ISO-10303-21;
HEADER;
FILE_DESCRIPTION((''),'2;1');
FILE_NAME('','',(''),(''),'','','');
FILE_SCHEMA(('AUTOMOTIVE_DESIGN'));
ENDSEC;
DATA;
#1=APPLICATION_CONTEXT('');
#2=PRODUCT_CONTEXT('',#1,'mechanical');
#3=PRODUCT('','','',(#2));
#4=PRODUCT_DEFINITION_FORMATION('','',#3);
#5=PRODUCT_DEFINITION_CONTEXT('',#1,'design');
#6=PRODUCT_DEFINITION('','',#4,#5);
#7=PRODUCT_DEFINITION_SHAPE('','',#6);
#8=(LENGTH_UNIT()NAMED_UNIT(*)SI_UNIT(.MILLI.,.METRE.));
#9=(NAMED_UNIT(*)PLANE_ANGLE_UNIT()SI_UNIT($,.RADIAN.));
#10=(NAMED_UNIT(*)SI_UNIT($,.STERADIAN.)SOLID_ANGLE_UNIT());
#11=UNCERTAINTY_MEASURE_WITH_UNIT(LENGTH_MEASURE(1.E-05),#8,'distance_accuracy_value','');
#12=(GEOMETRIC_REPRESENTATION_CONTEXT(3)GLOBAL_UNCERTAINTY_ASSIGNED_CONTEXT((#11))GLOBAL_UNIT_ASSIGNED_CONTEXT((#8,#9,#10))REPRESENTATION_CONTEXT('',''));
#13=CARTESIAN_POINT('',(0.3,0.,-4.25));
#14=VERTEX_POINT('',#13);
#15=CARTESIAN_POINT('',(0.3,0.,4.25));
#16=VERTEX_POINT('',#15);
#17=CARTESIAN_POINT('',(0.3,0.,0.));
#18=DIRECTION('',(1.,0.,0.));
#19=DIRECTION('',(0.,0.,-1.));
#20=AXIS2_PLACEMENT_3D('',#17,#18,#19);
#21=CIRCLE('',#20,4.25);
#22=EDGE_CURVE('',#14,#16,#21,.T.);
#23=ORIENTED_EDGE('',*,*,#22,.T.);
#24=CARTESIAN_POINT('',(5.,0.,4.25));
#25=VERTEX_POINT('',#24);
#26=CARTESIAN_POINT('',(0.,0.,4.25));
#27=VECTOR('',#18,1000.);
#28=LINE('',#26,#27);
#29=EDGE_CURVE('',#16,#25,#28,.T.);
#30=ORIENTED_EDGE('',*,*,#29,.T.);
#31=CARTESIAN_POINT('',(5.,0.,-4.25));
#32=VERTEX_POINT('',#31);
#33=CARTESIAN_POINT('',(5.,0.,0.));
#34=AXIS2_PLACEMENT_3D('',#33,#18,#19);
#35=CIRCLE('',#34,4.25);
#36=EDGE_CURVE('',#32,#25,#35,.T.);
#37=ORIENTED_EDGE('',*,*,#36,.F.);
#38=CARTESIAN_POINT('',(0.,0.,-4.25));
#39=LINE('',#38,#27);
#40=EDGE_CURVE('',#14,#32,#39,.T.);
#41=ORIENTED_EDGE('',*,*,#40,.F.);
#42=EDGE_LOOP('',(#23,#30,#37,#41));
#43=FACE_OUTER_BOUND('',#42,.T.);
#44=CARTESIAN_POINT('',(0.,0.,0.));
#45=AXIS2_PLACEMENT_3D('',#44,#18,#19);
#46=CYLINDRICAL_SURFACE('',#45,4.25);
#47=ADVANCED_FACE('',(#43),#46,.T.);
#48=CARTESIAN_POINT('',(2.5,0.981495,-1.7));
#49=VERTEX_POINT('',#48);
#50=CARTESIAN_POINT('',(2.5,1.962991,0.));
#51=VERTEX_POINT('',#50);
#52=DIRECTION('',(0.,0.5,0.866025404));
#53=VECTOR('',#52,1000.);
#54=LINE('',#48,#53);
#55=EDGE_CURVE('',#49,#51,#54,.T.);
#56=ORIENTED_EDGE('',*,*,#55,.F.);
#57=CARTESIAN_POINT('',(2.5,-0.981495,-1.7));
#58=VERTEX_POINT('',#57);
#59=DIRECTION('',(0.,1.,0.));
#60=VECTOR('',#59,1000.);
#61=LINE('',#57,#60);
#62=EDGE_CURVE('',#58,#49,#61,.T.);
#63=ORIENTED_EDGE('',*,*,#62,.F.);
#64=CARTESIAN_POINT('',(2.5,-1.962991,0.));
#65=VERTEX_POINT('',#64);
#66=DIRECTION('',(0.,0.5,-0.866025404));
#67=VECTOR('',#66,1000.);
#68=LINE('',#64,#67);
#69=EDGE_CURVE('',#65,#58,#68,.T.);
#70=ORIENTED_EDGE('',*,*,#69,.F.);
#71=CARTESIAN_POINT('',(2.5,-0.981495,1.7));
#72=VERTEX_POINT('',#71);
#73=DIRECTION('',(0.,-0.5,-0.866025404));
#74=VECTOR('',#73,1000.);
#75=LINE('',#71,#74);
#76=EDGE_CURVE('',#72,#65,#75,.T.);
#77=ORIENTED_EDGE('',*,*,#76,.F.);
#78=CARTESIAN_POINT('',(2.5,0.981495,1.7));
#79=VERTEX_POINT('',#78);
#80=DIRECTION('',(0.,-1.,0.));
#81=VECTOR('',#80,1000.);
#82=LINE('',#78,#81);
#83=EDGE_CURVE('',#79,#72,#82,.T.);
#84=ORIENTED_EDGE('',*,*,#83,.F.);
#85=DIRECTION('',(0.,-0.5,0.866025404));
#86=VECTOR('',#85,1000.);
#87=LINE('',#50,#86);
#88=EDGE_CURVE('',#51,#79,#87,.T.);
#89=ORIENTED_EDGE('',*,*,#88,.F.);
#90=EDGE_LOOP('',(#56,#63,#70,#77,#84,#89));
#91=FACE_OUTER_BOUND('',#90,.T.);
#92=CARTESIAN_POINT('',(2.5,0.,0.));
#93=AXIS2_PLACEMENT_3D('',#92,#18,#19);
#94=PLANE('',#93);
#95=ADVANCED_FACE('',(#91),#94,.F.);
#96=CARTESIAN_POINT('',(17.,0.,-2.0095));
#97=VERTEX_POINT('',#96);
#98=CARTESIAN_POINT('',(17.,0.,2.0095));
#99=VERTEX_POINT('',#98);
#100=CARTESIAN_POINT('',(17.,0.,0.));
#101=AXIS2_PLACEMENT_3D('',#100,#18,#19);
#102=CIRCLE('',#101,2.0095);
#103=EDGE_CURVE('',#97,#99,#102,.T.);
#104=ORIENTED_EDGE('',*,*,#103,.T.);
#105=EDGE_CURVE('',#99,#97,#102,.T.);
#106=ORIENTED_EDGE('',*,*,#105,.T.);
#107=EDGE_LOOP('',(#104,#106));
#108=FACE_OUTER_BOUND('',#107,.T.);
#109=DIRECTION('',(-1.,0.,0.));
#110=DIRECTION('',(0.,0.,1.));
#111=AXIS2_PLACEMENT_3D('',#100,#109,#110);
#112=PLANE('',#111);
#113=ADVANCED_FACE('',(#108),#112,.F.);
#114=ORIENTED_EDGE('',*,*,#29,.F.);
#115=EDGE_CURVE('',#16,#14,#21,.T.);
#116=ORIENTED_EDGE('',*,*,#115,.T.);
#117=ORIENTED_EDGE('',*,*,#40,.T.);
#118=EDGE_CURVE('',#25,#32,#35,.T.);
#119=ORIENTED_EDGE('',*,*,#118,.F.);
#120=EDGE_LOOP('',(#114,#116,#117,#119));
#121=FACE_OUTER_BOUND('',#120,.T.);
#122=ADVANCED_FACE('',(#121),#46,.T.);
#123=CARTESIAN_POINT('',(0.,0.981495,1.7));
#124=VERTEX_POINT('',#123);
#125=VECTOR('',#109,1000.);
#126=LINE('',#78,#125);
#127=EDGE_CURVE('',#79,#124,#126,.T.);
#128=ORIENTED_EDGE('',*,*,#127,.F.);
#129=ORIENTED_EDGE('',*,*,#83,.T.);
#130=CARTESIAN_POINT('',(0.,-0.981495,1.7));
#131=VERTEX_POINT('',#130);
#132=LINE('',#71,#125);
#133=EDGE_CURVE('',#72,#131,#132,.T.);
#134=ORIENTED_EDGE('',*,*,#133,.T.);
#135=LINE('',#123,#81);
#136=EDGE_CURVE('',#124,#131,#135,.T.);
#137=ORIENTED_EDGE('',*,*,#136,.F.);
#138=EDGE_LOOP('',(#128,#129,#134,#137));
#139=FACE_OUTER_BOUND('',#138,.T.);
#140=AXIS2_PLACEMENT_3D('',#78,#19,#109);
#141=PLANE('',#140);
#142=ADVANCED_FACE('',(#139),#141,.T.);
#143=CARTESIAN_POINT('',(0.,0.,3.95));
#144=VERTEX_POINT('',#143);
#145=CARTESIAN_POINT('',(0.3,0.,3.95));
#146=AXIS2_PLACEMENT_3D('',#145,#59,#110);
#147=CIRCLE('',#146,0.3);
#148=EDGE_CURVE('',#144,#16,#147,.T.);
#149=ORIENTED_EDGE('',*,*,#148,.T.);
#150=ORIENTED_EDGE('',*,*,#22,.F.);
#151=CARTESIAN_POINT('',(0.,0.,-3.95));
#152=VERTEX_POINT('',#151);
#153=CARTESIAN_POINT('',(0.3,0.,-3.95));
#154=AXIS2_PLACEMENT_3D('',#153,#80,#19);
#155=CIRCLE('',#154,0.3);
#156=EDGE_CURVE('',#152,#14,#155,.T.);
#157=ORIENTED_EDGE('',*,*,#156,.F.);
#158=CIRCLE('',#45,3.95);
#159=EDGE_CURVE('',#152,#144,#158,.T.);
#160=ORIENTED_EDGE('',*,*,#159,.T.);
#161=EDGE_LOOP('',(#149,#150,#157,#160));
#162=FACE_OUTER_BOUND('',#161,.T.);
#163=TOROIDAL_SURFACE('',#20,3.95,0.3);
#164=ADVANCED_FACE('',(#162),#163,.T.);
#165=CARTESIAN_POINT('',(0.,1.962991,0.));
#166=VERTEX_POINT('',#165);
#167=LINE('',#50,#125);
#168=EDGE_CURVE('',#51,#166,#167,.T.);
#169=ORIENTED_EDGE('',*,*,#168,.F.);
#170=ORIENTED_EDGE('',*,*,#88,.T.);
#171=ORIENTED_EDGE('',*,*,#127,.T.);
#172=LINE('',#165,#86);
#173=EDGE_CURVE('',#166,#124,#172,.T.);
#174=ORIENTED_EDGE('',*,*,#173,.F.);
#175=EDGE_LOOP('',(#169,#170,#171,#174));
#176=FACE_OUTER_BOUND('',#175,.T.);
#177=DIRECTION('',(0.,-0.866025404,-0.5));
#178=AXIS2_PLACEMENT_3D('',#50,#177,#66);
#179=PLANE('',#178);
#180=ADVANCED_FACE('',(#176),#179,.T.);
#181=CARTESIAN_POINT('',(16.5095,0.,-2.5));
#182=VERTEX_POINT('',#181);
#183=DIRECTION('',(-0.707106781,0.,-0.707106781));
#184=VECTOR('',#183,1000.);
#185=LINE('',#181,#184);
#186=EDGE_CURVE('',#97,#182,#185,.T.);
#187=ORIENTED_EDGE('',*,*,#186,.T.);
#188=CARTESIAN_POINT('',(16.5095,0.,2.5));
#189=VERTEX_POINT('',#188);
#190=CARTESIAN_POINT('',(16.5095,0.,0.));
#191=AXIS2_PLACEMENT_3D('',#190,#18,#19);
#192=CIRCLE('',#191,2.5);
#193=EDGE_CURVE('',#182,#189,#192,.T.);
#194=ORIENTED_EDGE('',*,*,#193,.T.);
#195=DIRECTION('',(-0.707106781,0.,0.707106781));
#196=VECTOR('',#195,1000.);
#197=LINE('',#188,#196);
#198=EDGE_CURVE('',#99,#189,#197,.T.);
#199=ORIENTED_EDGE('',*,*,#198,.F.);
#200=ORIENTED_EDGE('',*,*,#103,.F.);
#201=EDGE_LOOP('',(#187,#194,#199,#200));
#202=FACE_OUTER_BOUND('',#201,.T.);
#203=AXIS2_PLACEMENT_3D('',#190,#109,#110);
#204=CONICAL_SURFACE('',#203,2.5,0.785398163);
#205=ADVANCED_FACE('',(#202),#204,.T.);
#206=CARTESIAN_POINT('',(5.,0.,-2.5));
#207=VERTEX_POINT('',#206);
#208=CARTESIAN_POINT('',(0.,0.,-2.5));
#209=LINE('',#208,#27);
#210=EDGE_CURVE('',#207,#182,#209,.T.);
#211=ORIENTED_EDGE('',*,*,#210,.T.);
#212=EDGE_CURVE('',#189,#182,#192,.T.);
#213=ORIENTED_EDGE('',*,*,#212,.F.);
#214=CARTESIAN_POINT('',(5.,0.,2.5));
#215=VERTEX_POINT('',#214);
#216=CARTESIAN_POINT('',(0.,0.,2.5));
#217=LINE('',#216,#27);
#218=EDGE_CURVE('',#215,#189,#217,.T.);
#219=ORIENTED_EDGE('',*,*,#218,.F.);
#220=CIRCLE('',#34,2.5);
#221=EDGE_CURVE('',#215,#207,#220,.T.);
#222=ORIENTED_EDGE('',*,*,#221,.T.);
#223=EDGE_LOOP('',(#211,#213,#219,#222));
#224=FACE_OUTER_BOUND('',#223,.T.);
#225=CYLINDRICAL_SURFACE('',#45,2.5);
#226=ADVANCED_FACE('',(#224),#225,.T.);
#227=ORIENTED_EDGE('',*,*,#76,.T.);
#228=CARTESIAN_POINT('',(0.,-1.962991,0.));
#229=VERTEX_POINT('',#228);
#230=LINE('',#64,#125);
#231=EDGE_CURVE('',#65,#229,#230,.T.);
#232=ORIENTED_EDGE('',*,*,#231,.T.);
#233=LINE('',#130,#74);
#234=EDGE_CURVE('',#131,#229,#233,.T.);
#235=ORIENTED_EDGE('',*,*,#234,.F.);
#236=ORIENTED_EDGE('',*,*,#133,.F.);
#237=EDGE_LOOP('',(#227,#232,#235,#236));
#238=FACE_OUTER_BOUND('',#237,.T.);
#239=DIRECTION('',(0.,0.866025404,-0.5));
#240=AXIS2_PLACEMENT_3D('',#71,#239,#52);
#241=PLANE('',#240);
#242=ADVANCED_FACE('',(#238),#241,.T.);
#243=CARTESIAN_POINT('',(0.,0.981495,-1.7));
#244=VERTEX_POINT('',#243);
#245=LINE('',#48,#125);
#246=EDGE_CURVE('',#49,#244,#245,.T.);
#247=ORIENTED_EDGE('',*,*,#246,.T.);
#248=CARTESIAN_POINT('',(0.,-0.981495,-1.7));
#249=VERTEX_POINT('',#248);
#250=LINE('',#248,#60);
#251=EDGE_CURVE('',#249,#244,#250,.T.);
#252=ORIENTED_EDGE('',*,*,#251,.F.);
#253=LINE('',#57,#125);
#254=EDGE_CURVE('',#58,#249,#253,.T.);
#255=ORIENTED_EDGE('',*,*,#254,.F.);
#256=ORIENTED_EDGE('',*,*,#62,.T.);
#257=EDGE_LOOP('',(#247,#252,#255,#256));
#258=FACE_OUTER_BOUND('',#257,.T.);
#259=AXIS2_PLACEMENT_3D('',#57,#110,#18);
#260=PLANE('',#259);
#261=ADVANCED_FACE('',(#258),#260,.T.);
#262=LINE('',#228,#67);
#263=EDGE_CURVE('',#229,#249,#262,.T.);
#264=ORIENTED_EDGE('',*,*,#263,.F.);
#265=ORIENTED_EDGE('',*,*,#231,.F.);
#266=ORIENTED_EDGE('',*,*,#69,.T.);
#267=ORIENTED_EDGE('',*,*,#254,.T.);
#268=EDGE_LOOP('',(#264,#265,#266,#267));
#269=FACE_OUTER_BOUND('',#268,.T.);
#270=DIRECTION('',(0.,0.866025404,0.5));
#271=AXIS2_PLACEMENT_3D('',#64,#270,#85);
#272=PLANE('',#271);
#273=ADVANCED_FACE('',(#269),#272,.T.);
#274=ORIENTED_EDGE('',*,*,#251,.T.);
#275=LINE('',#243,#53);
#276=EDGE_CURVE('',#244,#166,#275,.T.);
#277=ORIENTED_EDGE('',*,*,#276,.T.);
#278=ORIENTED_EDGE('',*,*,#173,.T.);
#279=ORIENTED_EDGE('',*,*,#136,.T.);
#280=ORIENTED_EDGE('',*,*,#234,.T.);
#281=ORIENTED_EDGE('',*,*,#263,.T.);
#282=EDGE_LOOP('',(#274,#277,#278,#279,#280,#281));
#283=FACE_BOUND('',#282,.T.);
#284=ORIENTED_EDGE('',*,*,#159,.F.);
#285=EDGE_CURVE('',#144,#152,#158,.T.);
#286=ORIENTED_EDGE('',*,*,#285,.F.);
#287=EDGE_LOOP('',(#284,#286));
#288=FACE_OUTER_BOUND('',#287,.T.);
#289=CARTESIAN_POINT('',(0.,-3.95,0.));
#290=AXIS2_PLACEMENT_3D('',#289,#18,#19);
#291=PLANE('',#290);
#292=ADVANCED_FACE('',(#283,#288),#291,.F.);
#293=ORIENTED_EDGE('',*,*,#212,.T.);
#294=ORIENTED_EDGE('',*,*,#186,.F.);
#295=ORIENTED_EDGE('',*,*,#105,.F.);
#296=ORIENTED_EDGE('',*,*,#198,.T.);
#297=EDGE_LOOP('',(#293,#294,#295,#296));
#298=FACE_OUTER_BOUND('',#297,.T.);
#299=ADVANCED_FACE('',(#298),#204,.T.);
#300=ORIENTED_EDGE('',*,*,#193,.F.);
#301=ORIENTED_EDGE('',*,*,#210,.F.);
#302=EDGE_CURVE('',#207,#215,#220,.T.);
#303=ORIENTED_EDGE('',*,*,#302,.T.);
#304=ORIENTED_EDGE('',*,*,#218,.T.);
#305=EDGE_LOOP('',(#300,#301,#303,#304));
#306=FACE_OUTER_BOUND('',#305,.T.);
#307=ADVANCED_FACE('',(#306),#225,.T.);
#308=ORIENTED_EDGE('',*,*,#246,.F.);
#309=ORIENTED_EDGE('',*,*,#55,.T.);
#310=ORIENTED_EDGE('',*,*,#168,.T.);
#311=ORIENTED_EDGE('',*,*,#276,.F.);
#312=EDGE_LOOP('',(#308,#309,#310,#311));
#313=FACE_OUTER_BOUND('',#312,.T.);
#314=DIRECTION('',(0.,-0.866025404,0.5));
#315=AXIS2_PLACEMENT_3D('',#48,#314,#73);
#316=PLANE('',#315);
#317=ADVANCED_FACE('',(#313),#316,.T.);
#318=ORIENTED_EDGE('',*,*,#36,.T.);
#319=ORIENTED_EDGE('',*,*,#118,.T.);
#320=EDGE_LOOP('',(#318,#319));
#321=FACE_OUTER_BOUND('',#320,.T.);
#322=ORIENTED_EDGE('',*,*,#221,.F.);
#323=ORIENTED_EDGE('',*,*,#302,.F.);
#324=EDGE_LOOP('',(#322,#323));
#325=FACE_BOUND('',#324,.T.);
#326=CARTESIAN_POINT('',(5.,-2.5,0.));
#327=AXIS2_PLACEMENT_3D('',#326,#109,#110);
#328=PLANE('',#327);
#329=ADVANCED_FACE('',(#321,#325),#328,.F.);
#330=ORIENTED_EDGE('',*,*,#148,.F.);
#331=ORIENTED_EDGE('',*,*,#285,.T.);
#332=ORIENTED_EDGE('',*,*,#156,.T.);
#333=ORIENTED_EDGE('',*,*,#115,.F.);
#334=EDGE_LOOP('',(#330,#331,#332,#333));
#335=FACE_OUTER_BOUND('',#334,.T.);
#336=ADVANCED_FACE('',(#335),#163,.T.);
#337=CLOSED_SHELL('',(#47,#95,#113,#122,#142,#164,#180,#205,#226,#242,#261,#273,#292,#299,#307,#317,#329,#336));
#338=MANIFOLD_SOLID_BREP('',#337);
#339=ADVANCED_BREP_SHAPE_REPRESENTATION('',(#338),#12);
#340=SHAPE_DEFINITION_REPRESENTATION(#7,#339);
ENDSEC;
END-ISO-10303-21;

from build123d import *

# Parameters (mm, degrees)
CUT_EXTRUDE_1_DEPTH = 2.5


with BuildPart() as part:
    # 草图1 → 旋转1 (revolve)
    with BuildSketch(Plane.XY, mode=Mode.PRIVATE) as revolve_1_sk:
        with BuildLine():
            Line((17, 0), (17, -2.0095))
            Line((17, -2.0095), (16.5095, -2.5))
            Line((16.5095, -2.5), (5, -2.5))
            Line((5, -2.5), (5, -4.25))
            Line((5, -4.25), (0.3, -4.25))
            ThreePointArc((0.3, -4.25), (0.087867966, -4.162132034), (0, -3.95))
            Line((0, -3.95), (0, 0))
            Line((0, 0), (17, 0))
        make_face()
    revolve(revolve_1_sk.sketch.rotate(Axis((0, 0, 0), (1, 0, 0)), 90), axis=Axis((0, 0, 0), (1, 0, 0)))

    # 草图2 → 切除-拉伸1 (cut)
    with BuildSketch(Plane(origin=(0, 0, 0), x_dir=(0, 0, -1), z_dir=(1, 0, 0))):
        Polygon((-1.7, -0.981495458), (0, -1.962990915), (1.7, -0.981495458), (1.7, 0.981495458), (0, 1.962990915), (-1.7, 0.981495458), align=None)
    extrude(amount=CUT_EXTRUDE_1_DEPTH, mode=Mode.SUBTRACT)


solid = part.part
